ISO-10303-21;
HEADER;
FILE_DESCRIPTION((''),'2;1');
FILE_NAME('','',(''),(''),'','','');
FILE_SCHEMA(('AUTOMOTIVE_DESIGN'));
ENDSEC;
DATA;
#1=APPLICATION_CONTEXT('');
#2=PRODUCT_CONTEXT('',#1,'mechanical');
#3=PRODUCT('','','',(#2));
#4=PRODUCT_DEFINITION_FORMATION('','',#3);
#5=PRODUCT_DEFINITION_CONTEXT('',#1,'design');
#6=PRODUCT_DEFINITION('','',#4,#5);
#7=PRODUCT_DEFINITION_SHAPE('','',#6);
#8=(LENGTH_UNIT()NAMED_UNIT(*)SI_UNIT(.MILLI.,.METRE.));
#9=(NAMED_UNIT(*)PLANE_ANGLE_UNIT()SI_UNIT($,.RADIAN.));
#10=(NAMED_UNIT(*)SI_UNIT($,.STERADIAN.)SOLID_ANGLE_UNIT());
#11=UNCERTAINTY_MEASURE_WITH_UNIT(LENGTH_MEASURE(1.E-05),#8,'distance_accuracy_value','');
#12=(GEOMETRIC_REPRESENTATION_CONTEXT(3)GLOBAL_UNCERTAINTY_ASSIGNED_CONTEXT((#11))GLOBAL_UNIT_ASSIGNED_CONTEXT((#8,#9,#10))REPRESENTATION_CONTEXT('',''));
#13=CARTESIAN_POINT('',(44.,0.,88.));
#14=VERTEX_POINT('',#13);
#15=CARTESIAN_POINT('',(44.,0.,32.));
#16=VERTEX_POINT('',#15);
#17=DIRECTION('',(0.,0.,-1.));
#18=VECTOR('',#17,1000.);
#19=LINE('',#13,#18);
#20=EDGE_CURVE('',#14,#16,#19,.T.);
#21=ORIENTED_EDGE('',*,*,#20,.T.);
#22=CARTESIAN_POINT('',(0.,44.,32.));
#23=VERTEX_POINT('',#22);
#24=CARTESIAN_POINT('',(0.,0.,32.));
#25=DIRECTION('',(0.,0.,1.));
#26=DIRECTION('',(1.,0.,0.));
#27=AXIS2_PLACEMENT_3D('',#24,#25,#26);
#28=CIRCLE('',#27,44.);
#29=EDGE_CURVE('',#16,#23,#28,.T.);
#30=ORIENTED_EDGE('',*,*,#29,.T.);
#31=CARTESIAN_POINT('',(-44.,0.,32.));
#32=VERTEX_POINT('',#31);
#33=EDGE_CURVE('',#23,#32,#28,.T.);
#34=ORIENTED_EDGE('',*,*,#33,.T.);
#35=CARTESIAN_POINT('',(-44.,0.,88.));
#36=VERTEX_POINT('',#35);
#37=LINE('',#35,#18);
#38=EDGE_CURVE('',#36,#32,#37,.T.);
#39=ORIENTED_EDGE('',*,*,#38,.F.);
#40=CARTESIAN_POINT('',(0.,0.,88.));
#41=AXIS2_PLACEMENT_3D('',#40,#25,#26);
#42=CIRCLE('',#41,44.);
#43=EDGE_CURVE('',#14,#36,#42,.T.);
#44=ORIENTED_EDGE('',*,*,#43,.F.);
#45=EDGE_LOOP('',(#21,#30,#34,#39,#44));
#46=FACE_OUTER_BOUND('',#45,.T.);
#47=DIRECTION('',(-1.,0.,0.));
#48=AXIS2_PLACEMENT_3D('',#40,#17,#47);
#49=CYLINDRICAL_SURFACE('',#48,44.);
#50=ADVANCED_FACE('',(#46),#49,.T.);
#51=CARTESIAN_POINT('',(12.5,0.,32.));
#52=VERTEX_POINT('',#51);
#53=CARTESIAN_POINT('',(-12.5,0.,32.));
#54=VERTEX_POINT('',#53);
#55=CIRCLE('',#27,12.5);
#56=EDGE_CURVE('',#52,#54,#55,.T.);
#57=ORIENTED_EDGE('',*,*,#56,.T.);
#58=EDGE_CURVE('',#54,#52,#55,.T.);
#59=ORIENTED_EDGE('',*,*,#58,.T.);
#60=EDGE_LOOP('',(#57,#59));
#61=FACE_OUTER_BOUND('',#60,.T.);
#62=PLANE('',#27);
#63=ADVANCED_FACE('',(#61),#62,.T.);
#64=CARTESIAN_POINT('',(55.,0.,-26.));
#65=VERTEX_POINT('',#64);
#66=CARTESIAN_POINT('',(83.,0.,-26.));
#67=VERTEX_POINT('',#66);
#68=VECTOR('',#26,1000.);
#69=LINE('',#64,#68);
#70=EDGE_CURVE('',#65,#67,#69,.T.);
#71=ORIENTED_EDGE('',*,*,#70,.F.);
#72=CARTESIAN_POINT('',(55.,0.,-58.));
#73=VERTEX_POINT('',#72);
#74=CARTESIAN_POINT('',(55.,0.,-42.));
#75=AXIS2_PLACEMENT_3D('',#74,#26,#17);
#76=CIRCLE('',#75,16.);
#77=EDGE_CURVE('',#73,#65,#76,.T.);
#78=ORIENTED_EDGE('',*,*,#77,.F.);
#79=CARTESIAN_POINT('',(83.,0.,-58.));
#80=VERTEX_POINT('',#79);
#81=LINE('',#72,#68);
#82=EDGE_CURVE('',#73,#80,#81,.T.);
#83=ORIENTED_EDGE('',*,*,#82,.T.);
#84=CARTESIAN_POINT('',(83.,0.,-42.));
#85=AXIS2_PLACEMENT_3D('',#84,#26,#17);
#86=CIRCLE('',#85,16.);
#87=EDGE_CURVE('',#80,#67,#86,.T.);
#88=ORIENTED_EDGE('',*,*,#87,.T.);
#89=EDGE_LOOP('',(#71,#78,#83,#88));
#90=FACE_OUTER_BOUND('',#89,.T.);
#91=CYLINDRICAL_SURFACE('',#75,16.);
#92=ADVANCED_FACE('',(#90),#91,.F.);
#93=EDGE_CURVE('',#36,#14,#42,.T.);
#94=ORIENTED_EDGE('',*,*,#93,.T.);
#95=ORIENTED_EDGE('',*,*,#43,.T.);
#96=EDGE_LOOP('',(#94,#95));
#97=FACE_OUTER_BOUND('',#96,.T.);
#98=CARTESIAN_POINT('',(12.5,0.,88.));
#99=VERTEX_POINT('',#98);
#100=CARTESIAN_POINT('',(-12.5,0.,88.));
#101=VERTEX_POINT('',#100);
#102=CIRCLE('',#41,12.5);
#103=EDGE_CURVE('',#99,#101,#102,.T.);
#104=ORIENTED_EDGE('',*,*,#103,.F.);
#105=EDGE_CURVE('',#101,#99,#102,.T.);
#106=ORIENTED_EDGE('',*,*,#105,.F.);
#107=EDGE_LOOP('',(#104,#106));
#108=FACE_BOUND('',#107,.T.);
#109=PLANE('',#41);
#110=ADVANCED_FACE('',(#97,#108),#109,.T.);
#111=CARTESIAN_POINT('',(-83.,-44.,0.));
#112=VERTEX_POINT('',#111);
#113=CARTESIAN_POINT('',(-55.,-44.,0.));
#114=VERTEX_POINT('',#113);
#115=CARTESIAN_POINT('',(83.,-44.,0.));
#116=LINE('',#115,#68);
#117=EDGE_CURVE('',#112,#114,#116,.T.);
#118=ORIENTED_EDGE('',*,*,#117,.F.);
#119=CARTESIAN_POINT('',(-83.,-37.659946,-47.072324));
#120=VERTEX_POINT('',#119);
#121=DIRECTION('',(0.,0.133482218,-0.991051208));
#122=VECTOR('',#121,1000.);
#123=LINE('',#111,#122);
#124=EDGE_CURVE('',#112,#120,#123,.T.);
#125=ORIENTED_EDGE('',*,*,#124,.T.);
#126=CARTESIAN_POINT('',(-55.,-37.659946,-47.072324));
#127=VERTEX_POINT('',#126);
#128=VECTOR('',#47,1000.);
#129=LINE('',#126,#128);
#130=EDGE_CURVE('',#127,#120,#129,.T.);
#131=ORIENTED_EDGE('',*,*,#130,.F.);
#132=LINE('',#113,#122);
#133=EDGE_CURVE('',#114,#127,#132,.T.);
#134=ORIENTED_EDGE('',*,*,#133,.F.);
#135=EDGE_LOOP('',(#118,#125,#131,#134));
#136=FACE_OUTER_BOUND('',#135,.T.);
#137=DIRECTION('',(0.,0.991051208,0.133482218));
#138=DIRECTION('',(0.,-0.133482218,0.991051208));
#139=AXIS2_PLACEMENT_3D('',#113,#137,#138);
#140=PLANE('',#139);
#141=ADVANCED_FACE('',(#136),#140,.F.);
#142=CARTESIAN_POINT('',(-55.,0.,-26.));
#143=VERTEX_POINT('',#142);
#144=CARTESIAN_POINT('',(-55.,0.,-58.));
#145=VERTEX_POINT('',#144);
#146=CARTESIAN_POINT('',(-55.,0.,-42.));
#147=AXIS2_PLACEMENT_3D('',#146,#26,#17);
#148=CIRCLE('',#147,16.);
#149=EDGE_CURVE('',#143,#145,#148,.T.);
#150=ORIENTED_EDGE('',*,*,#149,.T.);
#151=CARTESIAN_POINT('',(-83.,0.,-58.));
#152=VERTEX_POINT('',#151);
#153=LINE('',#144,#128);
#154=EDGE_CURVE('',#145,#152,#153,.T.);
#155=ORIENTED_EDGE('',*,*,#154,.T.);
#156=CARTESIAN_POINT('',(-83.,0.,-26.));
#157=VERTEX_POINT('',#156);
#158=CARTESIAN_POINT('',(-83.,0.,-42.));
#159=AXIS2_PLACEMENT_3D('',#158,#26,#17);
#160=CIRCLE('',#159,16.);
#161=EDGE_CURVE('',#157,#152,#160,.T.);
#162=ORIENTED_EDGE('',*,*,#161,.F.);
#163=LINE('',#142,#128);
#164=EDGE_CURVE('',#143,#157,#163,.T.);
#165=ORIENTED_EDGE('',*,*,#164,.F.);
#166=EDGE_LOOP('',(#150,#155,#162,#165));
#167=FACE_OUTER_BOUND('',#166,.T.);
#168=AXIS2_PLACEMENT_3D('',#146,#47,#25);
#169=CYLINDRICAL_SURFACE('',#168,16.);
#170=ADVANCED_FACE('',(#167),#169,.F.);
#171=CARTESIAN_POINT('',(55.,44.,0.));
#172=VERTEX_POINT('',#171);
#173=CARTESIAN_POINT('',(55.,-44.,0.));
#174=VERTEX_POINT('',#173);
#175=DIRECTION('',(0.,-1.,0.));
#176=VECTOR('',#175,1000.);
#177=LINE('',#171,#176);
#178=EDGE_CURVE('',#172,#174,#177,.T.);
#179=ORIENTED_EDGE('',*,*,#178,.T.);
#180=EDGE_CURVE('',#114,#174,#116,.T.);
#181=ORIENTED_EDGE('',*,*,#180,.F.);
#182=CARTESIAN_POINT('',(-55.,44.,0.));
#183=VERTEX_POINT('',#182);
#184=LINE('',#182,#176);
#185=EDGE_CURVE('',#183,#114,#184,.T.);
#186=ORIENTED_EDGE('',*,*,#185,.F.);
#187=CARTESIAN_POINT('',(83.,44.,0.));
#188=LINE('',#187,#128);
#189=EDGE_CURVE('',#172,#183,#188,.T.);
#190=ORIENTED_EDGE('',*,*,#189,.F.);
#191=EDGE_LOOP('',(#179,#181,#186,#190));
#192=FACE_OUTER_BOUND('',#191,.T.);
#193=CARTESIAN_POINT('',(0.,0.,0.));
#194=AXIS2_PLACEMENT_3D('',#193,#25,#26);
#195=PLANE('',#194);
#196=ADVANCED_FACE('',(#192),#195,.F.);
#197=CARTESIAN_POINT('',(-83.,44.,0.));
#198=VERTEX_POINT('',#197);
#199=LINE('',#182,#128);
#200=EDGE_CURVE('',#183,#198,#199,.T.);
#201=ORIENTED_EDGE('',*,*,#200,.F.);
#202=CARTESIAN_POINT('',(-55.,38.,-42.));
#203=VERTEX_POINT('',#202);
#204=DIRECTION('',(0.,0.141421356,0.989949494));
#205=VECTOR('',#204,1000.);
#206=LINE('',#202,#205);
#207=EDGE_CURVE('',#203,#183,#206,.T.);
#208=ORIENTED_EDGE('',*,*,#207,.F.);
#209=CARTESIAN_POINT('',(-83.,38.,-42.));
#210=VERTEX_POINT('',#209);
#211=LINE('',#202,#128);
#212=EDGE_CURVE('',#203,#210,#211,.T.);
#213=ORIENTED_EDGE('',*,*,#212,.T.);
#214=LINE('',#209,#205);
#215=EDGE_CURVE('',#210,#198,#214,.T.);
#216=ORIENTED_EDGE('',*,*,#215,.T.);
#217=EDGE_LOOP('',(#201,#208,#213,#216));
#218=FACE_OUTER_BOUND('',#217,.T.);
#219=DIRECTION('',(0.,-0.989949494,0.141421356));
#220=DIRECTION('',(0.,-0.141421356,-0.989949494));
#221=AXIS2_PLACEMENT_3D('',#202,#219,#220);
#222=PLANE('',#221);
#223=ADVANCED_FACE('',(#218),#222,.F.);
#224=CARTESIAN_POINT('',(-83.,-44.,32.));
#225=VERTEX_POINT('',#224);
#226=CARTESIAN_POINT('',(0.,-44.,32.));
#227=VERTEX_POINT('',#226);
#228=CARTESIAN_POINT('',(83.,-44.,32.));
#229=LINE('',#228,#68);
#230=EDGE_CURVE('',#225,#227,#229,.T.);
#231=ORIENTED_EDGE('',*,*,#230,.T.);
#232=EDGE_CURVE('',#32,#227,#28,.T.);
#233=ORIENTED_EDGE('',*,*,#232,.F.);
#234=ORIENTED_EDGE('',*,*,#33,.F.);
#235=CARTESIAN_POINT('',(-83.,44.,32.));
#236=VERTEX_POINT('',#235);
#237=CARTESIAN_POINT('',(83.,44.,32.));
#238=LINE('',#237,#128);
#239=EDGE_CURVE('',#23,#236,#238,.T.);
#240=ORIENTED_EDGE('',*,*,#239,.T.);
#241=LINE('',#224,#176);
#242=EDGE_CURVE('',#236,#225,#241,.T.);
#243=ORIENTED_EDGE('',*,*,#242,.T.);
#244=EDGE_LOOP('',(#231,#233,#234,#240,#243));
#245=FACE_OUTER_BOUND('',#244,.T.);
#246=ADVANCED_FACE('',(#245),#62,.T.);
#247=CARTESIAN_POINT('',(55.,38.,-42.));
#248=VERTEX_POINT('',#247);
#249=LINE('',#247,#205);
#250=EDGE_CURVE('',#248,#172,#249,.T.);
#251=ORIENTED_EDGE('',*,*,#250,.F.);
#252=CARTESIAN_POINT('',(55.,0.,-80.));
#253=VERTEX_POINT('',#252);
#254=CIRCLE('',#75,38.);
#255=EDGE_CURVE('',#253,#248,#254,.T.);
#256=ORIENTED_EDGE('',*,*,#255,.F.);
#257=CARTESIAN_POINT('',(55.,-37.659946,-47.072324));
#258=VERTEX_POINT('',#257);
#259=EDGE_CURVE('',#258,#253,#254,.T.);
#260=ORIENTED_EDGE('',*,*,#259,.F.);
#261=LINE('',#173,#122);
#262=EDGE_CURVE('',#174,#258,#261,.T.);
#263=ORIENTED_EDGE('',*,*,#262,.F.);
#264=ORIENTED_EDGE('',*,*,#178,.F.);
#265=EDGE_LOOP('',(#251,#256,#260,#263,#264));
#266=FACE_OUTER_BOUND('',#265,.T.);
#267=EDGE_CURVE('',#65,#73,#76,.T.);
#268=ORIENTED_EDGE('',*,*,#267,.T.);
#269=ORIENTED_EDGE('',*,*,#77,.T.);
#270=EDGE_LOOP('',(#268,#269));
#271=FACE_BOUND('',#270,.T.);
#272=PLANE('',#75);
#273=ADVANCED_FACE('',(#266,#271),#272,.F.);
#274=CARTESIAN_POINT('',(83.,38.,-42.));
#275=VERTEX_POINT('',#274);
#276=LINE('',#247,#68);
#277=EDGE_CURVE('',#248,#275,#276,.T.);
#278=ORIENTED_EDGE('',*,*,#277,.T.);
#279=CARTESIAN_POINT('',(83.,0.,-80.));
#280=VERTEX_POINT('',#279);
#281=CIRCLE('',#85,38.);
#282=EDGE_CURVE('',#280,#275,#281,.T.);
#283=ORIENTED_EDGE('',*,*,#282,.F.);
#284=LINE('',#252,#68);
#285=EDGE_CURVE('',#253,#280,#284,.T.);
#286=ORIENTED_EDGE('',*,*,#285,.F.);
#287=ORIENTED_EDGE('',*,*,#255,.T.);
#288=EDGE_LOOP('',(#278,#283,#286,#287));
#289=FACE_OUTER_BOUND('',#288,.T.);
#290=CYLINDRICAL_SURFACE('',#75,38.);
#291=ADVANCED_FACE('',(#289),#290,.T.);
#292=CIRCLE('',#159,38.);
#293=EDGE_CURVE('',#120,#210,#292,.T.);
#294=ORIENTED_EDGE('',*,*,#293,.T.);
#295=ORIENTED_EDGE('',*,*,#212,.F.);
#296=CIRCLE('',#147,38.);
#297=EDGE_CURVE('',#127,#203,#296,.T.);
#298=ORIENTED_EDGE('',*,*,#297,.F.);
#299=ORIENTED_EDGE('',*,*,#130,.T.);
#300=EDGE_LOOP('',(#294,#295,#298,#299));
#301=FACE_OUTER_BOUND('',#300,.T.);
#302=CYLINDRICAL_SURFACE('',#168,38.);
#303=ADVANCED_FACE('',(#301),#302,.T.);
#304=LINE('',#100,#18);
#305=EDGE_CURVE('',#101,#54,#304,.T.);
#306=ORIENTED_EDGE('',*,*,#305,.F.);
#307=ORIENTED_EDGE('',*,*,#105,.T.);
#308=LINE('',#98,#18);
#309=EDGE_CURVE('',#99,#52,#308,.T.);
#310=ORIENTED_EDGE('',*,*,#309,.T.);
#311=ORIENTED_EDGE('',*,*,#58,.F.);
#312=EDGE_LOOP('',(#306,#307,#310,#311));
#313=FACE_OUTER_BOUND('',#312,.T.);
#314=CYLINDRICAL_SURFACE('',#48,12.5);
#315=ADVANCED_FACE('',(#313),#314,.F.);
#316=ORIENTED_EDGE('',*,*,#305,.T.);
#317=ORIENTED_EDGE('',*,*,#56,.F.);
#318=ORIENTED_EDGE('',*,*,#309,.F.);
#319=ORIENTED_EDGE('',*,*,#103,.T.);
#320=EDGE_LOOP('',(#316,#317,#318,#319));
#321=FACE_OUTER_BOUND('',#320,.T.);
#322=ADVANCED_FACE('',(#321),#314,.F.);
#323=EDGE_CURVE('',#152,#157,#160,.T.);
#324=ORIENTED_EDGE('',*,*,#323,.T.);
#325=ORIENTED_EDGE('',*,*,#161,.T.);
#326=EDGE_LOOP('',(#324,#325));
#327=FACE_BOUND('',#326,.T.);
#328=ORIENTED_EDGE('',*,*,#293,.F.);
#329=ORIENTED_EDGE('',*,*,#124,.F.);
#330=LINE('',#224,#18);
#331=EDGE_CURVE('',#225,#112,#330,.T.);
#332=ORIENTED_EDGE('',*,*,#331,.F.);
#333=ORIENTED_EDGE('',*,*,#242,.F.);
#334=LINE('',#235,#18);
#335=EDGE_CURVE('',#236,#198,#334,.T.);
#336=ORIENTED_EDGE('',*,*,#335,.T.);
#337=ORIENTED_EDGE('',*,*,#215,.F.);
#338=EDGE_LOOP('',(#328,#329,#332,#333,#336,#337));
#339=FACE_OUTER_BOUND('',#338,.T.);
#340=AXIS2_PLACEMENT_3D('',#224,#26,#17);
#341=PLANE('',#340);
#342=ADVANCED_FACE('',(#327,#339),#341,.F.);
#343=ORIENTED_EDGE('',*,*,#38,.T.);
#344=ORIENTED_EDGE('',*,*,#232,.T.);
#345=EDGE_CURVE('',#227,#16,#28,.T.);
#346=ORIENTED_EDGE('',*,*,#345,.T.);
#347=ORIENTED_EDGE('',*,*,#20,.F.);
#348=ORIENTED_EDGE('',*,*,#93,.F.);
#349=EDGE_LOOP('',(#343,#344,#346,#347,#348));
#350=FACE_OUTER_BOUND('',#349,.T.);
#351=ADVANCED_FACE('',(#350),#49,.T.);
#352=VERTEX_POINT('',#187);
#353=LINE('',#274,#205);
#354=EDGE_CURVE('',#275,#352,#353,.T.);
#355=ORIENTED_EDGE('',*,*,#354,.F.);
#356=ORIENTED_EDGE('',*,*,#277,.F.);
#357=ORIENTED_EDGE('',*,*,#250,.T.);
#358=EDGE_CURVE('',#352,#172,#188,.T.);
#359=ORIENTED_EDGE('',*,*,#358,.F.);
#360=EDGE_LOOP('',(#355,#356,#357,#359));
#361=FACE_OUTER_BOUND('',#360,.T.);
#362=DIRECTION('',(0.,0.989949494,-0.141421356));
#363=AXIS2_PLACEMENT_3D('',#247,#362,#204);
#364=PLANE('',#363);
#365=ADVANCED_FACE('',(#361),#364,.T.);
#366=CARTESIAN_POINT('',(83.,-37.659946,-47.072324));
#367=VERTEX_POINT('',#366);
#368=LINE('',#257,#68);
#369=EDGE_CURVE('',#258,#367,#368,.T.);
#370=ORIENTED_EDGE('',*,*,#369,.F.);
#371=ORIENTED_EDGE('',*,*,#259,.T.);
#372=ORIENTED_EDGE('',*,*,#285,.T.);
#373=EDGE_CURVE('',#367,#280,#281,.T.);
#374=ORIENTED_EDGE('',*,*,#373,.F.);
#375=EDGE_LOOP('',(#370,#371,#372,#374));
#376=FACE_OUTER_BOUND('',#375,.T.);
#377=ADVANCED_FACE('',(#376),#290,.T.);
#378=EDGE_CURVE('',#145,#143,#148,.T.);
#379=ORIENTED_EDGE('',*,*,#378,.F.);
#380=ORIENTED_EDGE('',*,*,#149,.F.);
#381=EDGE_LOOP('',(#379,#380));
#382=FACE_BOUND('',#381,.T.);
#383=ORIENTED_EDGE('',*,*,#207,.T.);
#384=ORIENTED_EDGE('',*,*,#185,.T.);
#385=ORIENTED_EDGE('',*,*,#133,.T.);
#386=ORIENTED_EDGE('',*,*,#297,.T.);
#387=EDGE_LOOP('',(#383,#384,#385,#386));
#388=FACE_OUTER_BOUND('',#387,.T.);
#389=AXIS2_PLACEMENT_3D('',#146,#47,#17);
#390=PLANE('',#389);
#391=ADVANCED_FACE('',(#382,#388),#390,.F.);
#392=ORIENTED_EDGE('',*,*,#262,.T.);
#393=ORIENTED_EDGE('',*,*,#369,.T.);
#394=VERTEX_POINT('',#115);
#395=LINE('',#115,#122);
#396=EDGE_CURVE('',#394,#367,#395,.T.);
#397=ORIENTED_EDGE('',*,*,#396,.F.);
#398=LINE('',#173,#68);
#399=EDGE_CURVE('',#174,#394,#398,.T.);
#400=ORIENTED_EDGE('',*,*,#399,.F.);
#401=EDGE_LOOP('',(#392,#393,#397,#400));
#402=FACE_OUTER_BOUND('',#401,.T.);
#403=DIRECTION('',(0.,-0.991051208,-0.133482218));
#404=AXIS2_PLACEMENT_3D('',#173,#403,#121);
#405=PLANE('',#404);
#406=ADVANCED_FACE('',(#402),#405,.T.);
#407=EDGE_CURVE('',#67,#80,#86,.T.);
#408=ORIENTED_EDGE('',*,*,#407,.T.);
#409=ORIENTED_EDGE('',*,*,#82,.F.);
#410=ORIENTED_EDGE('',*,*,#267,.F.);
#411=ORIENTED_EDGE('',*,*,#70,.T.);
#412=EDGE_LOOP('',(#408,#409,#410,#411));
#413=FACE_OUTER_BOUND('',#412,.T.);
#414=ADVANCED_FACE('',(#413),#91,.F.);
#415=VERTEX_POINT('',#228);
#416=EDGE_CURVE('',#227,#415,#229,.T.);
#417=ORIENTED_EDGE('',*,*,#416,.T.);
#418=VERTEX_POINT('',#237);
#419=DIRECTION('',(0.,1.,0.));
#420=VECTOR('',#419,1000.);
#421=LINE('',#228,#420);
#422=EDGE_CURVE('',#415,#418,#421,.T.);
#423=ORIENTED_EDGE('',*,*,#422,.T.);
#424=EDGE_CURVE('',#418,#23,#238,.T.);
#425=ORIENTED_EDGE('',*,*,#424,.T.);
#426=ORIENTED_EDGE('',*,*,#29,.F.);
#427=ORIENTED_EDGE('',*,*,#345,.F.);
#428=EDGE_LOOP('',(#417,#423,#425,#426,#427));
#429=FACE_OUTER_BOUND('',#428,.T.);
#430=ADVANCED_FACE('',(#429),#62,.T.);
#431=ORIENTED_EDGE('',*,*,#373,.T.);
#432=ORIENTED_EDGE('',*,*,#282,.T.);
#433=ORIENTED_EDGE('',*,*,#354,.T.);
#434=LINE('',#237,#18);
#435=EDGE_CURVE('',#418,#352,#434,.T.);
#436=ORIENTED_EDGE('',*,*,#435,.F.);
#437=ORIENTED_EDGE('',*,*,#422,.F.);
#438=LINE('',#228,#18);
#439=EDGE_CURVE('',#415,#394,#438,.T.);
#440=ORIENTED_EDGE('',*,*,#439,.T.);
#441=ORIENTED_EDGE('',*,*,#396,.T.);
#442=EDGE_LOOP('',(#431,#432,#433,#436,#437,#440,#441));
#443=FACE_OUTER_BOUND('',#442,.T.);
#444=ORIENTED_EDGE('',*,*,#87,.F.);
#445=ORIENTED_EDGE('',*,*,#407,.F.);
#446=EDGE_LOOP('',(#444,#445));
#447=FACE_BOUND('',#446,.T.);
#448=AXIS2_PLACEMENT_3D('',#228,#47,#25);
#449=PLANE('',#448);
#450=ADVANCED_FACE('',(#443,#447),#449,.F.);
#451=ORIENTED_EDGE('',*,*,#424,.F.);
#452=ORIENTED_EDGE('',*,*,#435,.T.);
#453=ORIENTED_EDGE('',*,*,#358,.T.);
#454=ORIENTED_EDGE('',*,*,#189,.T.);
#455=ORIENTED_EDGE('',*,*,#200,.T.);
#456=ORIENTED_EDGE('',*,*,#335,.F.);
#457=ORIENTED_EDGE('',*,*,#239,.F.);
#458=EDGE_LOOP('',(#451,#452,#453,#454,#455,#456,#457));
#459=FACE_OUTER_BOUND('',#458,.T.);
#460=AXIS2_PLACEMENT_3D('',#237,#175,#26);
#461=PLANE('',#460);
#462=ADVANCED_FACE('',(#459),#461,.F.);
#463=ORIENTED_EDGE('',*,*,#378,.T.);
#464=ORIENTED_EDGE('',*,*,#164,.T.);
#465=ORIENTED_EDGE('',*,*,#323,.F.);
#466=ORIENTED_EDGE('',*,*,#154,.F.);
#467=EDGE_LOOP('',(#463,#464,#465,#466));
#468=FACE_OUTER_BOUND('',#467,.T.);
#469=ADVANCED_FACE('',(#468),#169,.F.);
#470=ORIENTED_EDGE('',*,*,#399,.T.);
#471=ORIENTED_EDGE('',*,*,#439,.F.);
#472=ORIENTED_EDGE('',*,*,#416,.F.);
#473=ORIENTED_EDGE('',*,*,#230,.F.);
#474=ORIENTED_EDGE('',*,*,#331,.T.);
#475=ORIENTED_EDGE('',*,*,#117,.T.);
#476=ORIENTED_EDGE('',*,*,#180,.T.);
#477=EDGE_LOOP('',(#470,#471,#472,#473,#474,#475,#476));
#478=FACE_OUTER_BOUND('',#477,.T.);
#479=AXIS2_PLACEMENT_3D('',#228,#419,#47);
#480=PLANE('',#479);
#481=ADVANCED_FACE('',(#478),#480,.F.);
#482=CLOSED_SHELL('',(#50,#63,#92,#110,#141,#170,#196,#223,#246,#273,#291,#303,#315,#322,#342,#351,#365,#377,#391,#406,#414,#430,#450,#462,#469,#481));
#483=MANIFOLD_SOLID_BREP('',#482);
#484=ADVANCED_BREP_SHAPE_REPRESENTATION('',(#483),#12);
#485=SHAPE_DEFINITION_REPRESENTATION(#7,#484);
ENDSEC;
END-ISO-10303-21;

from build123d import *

# Parameters (mm, degrees)
BASE_BLOCK_SKETCH_W         = 166
BASE_BLOCK_SKETCH_H         = 88
BASE_BLOCK_166X88X32_DEPTH  = 32
BORED_BOSS_SKETCH_R         = 44
BORED_BOSS_SKETCH_R_2       = 12.5
BORED_BOSS_88_BORE_25_DEPTH = 56
LUG_SKETCH_R                = 16
PIERCED_LUG_DEPTH           = 28


with BuildPart() as part:
    # Base Block Sketch → Base Block 166x88x32 (new body)
    with BuildSketch(Plane.XY):
        Rectangle(BASE_BLOCK_SKETCH_W, BASE_BLOCK_SKETCH_H)
    extrude(amount=BASE_BLOCK_166X88X32_DEPTH)

    # Bored Boss Sketch → Bored Boss Ø88 Bore Ø25 (add)
    with BuildSketch(Plane.XY.offset(32)):
        with Locations(Location((0, 0, 0), (0, 0, 270))):
            Circle(BORED_BOSS_SKETCH_R)
        Circle(BORED_BOSS_SKETCH_R_2, mode=Mode.SUBTRACT)
    extrude(amount=BORED_BOSS_88_BORE_25_DEPTH)

    # Lug Sketch → Pierced Lug (add)
    with BuildSketch(Plane(origin=(83, 0, 0), x_dir=(0, 0, -1), z_dir=(1, 0, 0))):
        with BuildLine():
            Line((0, 44), (0, -44))
            Line((0, -44), (47.072324291, -37.659945915))
            ThreePointArc((47.072324291, -37.659945915), (79.914891169, 2.541855154), (42, 38))
            Line((42, 38), (0, 44))
        make_face()
        with Locations((42, 0)):
            Circle(LUG_SKETCH_R, mode=Mode.SUBTRACT)
    pierced_lug = extrude(amount=-PIERCED_LUG_DEPTH)

    # Lug Mirror: Pierced Lug across plane
    add(pierced_lug.mirror(Plane(origin=(0, 0, 0), x_dir=(0, 0, 1), z_dir=(1, 0, 0))))


solid = part.part
